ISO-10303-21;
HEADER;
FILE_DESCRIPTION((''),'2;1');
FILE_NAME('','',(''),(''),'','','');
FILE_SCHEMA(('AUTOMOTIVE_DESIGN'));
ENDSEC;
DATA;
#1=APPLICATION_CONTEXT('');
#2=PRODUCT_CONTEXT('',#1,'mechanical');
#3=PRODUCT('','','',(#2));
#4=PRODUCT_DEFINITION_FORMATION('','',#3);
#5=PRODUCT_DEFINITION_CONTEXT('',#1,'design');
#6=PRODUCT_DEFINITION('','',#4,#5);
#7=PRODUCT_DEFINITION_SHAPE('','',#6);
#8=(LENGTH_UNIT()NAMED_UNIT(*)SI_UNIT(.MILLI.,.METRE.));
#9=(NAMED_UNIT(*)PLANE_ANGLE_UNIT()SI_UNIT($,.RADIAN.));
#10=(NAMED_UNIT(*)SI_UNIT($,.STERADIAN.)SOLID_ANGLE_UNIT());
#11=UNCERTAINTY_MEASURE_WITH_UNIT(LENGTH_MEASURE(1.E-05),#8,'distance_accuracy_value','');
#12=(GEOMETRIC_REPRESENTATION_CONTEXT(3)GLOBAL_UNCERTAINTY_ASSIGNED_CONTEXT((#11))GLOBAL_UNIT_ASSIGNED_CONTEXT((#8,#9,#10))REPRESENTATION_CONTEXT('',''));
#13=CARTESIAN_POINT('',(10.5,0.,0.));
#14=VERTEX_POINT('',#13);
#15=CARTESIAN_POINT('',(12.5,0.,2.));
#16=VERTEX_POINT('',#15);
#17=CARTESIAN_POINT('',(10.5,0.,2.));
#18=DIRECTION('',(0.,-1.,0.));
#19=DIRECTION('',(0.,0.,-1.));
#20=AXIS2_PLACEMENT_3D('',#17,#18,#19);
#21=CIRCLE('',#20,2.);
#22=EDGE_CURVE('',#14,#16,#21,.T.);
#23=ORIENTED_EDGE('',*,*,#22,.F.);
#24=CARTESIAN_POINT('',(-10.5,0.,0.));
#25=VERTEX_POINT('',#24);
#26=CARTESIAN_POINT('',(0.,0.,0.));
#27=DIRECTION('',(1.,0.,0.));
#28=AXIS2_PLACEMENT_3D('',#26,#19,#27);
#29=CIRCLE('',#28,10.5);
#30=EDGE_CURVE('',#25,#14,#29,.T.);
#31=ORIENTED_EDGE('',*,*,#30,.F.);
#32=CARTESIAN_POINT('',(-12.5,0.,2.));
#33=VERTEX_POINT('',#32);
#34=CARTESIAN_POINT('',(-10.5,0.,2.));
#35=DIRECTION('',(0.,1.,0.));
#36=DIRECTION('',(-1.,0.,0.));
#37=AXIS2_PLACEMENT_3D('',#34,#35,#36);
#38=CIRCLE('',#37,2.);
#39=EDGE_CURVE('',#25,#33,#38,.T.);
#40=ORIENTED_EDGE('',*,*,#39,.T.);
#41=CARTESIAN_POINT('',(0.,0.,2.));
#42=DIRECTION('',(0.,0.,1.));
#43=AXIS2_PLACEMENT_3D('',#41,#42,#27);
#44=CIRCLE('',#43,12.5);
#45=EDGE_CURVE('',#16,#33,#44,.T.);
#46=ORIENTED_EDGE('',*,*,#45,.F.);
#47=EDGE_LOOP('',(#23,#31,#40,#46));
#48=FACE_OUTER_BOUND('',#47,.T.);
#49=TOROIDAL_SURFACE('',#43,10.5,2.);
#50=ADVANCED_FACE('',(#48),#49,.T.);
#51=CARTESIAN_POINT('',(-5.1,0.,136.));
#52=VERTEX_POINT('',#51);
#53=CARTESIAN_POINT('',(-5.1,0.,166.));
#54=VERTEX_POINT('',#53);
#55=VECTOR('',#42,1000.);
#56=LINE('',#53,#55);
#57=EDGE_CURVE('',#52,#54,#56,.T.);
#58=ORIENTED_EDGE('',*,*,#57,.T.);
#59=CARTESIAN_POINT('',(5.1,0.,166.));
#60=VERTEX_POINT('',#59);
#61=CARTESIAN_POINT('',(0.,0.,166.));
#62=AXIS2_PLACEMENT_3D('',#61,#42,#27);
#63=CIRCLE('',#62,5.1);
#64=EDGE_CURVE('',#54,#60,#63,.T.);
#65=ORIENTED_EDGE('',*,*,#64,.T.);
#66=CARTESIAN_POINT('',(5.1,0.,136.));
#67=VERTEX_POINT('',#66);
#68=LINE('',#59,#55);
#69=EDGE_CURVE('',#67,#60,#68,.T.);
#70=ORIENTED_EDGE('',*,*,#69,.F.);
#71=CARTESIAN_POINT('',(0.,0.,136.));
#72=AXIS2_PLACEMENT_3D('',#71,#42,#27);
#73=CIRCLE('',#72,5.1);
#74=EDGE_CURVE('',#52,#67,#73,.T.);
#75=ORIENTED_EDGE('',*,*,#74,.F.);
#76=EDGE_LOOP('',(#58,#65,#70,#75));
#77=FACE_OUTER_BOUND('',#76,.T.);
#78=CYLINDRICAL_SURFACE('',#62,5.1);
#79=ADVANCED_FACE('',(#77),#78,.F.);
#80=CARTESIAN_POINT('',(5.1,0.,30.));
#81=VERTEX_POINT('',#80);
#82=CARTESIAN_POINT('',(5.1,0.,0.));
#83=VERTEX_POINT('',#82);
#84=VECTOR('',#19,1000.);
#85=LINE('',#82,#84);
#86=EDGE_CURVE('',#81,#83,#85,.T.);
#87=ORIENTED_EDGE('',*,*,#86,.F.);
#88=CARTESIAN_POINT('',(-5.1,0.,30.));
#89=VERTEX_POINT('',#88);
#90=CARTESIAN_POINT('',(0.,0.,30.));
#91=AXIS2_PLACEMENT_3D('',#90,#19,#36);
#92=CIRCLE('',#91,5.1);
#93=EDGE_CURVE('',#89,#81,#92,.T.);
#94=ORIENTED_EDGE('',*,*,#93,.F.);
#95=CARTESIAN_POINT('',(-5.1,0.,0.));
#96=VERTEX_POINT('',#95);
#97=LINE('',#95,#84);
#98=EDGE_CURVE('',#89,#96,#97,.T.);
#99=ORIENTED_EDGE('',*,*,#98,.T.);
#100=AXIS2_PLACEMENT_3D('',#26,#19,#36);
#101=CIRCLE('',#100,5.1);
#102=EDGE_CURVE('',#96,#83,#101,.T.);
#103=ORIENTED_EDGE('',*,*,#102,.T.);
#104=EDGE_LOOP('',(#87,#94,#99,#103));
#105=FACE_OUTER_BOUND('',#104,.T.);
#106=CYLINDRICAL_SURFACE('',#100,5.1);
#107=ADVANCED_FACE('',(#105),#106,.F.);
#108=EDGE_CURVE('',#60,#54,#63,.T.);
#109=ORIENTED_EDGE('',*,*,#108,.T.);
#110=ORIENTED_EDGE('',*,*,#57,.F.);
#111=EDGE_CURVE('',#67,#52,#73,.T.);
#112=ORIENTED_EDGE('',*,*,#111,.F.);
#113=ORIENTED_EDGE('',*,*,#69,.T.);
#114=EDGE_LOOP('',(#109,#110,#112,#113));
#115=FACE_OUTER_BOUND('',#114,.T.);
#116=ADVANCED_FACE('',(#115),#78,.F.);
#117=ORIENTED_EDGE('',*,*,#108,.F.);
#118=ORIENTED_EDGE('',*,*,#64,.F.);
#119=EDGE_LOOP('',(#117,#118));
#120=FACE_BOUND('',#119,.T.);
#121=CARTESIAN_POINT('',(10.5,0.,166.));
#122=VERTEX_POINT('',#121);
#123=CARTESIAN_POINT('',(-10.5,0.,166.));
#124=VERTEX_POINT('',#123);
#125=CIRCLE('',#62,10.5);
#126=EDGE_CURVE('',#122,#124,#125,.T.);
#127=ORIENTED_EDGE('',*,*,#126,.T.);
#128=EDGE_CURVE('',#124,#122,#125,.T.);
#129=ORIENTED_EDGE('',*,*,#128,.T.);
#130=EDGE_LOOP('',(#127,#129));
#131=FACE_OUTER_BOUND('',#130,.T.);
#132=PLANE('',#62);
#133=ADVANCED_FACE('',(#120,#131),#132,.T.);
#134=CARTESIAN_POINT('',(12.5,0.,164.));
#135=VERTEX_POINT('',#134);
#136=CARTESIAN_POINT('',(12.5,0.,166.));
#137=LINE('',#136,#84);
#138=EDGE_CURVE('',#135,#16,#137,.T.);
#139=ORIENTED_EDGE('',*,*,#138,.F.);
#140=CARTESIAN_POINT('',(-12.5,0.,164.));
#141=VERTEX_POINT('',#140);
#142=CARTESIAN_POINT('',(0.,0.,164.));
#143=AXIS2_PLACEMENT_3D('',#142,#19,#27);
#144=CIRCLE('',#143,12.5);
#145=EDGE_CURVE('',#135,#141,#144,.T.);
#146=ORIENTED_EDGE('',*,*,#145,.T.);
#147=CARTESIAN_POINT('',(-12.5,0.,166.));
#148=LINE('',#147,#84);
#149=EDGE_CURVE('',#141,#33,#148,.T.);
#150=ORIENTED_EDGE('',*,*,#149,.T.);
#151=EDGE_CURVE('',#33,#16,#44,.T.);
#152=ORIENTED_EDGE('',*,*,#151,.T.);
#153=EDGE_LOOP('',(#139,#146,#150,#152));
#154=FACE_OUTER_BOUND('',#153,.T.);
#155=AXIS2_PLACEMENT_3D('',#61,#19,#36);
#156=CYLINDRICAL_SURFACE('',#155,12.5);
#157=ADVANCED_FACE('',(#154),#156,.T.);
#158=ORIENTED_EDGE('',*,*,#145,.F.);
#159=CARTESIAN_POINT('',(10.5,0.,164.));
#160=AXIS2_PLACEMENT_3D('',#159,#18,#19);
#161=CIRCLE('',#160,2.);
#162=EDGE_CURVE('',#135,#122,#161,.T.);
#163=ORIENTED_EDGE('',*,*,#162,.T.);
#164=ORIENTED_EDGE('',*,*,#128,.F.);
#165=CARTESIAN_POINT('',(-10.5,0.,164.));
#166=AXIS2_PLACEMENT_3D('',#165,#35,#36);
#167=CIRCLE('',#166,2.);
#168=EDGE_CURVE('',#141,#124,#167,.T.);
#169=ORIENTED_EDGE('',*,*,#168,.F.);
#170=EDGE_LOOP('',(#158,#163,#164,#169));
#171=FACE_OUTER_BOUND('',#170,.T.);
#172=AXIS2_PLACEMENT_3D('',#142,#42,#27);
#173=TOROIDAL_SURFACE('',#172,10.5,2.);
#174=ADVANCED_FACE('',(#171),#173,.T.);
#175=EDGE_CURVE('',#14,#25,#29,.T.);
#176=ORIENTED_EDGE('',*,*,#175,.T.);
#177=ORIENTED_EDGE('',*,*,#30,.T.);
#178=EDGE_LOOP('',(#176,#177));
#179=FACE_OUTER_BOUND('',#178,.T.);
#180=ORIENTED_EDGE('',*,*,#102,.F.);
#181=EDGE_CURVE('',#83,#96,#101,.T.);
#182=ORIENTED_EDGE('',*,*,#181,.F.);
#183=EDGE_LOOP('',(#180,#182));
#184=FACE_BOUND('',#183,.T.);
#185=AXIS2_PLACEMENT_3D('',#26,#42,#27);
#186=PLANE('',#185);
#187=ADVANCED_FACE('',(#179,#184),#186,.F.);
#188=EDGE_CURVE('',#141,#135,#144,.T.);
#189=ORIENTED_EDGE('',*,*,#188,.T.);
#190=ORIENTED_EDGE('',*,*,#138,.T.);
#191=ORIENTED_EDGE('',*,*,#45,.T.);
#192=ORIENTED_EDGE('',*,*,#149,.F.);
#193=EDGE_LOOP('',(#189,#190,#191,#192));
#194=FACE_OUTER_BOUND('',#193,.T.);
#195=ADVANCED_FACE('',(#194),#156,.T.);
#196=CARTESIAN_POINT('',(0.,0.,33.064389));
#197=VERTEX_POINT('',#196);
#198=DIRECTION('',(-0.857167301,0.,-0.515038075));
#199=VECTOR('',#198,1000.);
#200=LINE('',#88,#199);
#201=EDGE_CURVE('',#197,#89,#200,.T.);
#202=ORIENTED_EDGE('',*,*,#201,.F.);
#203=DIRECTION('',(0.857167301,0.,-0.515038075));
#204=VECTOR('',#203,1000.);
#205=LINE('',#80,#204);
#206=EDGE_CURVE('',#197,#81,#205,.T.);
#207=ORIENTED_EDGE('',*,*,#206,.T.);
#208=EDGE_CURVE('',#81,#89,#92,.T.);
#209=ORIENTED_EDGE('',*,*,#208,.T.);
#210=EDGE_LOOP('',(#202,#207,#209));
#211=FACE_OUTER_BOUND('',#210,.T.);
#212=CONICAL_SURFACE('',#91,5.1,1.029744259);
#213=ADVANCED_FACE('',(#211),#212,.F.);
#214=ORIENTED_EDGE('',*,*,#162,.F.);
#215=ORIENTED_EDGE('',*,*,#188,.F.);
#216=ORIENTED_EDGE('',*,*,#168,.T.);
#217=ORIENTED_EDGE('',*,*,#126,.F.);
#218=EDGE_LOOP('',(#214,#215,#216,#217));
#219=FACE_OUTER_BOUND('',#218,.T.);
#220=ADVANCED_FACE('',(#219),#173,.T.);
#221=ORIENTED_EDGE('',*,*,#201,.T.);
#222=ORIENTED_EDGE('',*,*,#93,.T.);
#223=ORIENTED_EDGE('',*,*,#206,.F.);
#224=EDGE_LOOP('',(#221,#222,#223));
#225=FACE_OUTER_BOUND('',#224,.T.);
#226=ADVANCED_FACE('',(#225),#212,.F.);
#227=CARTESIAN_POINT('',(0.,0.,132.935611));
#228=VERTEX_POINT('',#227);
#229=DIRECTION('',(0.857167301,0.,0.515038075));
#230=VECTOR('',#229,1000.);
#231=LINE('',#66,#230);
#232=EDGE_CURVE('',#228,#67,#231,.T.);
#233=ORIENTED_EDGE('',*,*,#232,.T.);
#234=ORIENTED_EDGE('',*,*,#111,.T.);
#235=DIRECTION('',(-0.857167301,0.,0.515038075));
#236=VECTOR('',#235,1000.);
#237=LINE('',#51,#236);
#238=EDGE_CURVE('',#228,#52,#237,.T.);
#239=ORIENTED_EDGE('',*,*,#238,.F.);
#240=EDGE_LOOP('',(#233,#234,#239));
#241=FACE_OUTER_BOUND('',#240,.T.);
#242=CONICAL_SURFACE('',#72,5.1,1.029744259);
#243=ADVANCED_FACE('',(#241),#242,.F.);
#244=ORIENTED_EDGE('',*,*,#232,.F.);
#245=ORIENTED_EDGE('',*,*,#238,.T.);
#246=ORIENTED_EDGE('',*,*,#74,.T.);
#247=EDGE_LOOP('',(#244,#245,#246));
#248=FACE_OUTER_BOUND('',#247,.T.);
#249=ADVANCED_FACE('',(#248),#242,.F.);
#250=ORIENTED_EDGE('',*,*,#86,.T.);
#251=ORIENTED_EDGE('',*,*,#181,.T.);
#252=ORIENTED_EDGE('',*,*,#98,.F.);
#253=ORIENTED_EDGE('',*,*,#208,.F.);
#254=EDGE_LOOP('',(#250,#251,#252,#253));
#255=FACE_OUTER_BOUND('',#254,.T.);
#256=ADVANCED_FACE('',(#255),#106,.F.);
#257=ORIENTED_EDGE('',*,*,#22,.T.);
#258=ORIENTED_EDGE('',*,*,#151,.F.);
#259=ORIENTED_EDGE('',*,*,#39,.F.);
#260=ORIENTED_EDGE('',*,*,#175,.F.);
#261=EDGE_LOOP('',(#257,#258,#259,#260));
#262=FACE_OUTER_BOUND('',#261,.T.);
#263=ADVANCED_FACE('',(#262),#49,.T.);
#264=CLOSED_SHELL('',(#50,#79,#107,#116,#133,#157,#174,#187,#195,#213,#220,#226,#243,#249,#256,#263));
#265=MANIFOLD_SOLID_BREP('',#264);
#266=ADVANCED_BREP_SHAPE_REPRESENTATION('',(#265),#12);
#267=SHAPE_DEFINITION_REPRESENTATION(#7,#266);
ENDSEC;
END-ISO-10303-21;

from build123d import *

# Parameters (mm, degrees)
SKETCH1_R              = 12.5
BOSS_EXTRUDE1_DEPTH    = 166
FILLET1_R              = 2
M12_TAPPED_HOLE1_D     = 10.2
M12_TAPPED_HOLE1_DEPTH = 30
M12_TAPPED_HOLE1_TIP   = 3.064389157
M12_TAPPED_HOLE2_D     = 10.2
M12_TAPPED_HOLE2_DEPTH = 30
M12_TAPPED_HOLE2_TIP   = 3.064389157


with BuildPart() as part:
    # Sketch1 → Boss-Extrude1 (new body)
    with BuildSketch(Plane.XY):
        Circle(SKETCH1_R)
    extrude(amount=BOSS_EXTRUDE1_DEPTH)

    # Fillet1
    fillet1_edges = [part.edges().sort_by_distance(p)[0] for p in [
        (-12.5, 0, 0),
        (-12.5, 0, 166),
    ]]
    fillet(fillet1_edges, radius=FILLET1_R)

    # M12 Tapped Hole1
    with Locations(Plane.XY.offset(166)):
        with Locations((0, 0)):
            Hole(M12_TAPPED_HOLE1_D / 2, depth=M12_TAPPED_HOLE1_DEPTH)
            with Locations((0, 0, -(M12_TAPPED_HOLE1_DEPTH + M12_TAPPED_HOLE1_TIP / 2))):  # 118° drill point
                Cone(0, M12_TAPPED_HOLE1_D / 2, M12_TAPPED_HOLE1_TIP, mode=Mode.SUBTRACT)

    # M12 Tapped Hole2
    with Locations(Plane(origin=(0, 0, 0), x_dir=(-1, 0, 0), z_dir=(0, 0, -1))):
        with Locations((0, 0)):
            Hole(M12_TAPPED_HOLE2_D / 2, depth=M12_TAPPED_HOLE2_DEPTH)
            with Locations((0, 0, -(M12_TAPPED_HOLE2_DEPTH + M12_TAPPED_HOLE2_TIP / 2))):  # 118° drill point
                Cone(0, M12_TAPPED_HOLE2_D / 2, M12_TAPPED_HOLE2_TIP, mode=Mode.SUBTRACT)


solid = part.part
